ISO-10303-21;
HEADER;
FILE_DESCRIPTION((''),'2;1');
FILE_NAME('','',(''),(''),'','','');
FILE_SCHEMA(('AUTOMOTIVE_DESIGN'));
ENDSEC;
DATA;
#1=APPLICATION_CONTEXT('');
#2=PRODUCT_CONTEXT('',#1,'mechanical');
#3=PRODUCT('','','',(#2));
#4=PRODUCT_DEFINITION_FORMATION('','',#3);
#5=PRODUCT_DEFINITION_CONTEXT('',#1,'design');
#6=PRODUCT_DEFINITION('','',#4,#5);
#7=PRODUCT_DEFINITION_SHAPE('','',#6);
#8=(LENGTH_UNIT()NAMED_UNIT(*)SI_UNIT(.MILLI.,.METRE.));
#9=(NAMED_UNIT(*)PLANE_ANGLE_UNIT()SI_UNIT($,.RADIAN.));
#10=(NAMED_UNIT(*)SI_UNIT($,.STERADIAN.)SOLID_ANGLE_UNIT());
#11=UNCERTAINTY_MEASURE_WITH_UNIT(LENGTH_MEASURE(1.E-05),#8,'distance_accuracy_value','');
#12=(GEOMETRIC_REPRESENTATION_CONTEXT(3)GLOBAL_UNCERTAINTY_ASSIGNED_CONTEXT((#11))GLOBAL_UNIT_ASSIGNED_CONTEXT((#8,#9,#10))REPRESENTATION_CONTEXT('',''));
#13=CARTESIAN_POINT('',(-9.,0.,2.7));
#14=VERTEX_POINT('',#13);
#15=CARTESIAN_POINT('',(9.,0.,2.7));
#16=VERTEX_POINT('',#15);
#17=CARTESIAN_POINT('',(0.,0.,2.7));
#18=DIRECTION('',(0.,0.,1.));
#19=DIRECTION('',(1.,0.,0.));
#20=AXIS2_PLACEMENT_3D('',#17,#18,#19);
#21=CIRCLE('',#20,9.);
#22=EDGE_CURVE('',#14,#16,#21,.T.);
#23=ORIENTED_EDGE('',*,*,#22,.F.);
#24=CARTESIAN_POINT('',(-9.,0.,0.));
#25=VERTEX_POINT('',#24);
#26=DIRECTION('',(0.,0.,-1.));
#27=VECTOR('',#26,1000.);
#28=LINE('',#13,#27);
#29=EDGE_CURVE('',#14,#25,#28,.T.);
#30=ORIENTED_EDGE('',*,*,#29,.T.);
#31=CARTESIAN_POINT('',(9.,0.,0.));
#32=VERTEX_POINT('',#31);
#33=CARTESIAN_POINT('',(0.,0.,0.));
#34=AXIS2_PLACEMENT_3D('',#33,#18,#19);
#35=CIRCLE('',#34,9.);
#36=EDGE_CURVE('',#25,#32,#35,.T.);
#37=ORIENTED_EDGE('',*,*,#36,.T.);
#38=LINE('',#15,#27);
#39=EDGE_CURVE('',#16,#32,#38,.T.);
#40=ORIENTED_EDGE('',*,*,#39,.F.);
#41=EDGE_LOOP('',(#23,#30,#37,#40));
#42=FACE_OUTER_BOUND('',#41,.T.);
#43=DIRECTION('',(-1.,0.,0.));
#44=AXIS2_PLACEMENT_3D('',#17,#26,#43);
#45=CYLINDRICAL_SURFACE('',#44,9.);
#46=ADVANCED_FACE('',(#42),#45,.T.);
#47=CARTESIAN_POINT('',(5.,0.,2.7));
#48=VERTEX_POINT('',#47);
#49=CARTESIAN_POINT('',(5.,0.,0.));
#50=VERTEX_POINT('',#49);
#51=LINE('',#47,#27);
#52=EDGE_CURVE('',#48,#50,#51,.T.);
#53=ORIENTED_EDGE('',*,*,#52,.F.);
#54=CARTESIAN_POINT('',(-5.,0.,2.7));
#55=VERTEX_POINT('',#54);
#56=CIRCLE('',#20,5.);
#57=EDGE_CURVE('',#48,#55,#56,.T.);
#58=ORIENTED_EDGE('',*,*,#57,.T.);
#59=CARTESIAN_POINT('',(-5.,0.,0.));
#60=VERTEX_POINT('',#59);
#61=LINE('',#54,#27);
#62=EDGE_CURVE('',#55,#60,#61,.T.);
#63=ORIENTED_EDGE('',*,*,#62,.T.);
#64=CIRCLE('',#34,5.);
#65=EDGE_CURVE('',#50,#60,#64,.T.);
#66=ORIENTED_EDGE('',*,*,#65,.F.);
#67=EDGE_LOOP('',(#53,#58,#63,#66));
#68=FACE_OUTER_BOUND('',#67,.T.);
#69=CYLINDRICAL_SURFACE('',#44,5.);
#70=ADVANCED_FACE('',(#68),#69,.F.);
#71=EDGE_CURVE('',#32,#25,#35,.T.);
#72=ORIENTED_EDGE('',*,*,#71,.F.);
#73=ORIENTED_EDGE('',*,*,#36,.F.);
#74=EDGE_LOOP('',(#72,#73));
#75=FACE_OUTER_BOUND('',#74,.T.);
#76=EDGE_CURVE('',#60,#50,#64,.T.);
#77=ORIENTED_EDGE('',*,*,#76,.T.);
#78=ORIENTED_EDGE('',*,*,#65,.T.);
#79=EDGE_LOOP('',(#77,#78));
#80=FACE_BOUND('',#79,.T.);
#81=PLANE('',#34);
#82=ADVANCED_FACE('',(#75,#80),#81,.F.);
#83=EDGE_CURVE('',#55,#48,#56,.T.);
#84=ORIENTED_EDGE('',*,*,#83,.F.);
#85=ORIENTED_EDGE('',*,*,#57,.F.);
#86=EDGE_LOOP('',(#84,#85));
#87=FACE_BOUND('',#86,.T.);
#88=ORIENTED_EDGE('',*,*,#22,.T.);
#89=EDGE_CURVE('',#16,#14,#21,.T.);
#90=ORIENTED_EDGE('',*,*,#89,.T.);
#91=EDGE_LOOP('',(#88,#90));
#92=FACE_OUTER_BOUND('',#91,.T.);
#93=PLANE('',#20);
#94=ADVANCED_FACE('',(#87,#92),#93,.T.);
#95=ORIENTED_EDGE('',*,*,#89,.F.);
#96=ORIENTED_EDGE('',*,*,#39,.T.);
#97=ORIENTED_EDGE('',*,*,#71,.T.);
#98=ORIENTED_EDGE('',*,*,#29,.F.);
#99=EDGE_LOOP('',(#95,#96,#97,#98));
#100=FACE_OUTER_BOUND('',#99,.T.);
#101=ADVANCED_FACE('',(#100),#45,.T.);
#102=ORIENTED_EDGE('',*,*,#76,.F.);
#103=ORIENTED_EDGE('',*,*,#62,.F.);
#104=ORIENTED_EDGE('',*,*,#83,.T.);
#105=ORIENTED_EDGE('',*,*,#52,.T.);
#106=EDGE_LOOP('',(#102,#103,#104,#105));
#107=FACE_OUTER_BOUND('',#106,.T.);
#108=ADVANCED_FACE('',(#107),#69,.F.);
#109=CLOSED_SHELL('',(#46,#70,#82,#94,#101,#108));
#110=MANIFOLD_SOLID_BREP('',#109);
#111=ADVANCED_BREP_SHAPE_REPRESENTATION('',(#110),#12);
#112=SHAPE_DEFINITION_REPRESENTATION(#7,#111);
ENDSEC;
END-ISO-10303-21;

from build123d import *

# Parameters (mm, degrees)
SKETCH1_R           = 9
SKETCH1_R_2         = 5
BOSS_EXTRUDE1_DEPTH = 2.7


with BuildPart() as part:
    # Sketch1 → Boss-Extrude1 (new body)
    with BuildSketch(Plane.XY):
        with Locations(Location((0, 0, 0), (0, 0, 180))):
            Circle(SKETCH1_R)
        with Locations(Location((0, 0, 0), (0, 0, 180))):
            Circle(SKETCH1_R_2, mode=Mode.SUBTRACT)
    extrude(amount=BOSS_EXTRUDE1_DEPTH)


solid = part.part
